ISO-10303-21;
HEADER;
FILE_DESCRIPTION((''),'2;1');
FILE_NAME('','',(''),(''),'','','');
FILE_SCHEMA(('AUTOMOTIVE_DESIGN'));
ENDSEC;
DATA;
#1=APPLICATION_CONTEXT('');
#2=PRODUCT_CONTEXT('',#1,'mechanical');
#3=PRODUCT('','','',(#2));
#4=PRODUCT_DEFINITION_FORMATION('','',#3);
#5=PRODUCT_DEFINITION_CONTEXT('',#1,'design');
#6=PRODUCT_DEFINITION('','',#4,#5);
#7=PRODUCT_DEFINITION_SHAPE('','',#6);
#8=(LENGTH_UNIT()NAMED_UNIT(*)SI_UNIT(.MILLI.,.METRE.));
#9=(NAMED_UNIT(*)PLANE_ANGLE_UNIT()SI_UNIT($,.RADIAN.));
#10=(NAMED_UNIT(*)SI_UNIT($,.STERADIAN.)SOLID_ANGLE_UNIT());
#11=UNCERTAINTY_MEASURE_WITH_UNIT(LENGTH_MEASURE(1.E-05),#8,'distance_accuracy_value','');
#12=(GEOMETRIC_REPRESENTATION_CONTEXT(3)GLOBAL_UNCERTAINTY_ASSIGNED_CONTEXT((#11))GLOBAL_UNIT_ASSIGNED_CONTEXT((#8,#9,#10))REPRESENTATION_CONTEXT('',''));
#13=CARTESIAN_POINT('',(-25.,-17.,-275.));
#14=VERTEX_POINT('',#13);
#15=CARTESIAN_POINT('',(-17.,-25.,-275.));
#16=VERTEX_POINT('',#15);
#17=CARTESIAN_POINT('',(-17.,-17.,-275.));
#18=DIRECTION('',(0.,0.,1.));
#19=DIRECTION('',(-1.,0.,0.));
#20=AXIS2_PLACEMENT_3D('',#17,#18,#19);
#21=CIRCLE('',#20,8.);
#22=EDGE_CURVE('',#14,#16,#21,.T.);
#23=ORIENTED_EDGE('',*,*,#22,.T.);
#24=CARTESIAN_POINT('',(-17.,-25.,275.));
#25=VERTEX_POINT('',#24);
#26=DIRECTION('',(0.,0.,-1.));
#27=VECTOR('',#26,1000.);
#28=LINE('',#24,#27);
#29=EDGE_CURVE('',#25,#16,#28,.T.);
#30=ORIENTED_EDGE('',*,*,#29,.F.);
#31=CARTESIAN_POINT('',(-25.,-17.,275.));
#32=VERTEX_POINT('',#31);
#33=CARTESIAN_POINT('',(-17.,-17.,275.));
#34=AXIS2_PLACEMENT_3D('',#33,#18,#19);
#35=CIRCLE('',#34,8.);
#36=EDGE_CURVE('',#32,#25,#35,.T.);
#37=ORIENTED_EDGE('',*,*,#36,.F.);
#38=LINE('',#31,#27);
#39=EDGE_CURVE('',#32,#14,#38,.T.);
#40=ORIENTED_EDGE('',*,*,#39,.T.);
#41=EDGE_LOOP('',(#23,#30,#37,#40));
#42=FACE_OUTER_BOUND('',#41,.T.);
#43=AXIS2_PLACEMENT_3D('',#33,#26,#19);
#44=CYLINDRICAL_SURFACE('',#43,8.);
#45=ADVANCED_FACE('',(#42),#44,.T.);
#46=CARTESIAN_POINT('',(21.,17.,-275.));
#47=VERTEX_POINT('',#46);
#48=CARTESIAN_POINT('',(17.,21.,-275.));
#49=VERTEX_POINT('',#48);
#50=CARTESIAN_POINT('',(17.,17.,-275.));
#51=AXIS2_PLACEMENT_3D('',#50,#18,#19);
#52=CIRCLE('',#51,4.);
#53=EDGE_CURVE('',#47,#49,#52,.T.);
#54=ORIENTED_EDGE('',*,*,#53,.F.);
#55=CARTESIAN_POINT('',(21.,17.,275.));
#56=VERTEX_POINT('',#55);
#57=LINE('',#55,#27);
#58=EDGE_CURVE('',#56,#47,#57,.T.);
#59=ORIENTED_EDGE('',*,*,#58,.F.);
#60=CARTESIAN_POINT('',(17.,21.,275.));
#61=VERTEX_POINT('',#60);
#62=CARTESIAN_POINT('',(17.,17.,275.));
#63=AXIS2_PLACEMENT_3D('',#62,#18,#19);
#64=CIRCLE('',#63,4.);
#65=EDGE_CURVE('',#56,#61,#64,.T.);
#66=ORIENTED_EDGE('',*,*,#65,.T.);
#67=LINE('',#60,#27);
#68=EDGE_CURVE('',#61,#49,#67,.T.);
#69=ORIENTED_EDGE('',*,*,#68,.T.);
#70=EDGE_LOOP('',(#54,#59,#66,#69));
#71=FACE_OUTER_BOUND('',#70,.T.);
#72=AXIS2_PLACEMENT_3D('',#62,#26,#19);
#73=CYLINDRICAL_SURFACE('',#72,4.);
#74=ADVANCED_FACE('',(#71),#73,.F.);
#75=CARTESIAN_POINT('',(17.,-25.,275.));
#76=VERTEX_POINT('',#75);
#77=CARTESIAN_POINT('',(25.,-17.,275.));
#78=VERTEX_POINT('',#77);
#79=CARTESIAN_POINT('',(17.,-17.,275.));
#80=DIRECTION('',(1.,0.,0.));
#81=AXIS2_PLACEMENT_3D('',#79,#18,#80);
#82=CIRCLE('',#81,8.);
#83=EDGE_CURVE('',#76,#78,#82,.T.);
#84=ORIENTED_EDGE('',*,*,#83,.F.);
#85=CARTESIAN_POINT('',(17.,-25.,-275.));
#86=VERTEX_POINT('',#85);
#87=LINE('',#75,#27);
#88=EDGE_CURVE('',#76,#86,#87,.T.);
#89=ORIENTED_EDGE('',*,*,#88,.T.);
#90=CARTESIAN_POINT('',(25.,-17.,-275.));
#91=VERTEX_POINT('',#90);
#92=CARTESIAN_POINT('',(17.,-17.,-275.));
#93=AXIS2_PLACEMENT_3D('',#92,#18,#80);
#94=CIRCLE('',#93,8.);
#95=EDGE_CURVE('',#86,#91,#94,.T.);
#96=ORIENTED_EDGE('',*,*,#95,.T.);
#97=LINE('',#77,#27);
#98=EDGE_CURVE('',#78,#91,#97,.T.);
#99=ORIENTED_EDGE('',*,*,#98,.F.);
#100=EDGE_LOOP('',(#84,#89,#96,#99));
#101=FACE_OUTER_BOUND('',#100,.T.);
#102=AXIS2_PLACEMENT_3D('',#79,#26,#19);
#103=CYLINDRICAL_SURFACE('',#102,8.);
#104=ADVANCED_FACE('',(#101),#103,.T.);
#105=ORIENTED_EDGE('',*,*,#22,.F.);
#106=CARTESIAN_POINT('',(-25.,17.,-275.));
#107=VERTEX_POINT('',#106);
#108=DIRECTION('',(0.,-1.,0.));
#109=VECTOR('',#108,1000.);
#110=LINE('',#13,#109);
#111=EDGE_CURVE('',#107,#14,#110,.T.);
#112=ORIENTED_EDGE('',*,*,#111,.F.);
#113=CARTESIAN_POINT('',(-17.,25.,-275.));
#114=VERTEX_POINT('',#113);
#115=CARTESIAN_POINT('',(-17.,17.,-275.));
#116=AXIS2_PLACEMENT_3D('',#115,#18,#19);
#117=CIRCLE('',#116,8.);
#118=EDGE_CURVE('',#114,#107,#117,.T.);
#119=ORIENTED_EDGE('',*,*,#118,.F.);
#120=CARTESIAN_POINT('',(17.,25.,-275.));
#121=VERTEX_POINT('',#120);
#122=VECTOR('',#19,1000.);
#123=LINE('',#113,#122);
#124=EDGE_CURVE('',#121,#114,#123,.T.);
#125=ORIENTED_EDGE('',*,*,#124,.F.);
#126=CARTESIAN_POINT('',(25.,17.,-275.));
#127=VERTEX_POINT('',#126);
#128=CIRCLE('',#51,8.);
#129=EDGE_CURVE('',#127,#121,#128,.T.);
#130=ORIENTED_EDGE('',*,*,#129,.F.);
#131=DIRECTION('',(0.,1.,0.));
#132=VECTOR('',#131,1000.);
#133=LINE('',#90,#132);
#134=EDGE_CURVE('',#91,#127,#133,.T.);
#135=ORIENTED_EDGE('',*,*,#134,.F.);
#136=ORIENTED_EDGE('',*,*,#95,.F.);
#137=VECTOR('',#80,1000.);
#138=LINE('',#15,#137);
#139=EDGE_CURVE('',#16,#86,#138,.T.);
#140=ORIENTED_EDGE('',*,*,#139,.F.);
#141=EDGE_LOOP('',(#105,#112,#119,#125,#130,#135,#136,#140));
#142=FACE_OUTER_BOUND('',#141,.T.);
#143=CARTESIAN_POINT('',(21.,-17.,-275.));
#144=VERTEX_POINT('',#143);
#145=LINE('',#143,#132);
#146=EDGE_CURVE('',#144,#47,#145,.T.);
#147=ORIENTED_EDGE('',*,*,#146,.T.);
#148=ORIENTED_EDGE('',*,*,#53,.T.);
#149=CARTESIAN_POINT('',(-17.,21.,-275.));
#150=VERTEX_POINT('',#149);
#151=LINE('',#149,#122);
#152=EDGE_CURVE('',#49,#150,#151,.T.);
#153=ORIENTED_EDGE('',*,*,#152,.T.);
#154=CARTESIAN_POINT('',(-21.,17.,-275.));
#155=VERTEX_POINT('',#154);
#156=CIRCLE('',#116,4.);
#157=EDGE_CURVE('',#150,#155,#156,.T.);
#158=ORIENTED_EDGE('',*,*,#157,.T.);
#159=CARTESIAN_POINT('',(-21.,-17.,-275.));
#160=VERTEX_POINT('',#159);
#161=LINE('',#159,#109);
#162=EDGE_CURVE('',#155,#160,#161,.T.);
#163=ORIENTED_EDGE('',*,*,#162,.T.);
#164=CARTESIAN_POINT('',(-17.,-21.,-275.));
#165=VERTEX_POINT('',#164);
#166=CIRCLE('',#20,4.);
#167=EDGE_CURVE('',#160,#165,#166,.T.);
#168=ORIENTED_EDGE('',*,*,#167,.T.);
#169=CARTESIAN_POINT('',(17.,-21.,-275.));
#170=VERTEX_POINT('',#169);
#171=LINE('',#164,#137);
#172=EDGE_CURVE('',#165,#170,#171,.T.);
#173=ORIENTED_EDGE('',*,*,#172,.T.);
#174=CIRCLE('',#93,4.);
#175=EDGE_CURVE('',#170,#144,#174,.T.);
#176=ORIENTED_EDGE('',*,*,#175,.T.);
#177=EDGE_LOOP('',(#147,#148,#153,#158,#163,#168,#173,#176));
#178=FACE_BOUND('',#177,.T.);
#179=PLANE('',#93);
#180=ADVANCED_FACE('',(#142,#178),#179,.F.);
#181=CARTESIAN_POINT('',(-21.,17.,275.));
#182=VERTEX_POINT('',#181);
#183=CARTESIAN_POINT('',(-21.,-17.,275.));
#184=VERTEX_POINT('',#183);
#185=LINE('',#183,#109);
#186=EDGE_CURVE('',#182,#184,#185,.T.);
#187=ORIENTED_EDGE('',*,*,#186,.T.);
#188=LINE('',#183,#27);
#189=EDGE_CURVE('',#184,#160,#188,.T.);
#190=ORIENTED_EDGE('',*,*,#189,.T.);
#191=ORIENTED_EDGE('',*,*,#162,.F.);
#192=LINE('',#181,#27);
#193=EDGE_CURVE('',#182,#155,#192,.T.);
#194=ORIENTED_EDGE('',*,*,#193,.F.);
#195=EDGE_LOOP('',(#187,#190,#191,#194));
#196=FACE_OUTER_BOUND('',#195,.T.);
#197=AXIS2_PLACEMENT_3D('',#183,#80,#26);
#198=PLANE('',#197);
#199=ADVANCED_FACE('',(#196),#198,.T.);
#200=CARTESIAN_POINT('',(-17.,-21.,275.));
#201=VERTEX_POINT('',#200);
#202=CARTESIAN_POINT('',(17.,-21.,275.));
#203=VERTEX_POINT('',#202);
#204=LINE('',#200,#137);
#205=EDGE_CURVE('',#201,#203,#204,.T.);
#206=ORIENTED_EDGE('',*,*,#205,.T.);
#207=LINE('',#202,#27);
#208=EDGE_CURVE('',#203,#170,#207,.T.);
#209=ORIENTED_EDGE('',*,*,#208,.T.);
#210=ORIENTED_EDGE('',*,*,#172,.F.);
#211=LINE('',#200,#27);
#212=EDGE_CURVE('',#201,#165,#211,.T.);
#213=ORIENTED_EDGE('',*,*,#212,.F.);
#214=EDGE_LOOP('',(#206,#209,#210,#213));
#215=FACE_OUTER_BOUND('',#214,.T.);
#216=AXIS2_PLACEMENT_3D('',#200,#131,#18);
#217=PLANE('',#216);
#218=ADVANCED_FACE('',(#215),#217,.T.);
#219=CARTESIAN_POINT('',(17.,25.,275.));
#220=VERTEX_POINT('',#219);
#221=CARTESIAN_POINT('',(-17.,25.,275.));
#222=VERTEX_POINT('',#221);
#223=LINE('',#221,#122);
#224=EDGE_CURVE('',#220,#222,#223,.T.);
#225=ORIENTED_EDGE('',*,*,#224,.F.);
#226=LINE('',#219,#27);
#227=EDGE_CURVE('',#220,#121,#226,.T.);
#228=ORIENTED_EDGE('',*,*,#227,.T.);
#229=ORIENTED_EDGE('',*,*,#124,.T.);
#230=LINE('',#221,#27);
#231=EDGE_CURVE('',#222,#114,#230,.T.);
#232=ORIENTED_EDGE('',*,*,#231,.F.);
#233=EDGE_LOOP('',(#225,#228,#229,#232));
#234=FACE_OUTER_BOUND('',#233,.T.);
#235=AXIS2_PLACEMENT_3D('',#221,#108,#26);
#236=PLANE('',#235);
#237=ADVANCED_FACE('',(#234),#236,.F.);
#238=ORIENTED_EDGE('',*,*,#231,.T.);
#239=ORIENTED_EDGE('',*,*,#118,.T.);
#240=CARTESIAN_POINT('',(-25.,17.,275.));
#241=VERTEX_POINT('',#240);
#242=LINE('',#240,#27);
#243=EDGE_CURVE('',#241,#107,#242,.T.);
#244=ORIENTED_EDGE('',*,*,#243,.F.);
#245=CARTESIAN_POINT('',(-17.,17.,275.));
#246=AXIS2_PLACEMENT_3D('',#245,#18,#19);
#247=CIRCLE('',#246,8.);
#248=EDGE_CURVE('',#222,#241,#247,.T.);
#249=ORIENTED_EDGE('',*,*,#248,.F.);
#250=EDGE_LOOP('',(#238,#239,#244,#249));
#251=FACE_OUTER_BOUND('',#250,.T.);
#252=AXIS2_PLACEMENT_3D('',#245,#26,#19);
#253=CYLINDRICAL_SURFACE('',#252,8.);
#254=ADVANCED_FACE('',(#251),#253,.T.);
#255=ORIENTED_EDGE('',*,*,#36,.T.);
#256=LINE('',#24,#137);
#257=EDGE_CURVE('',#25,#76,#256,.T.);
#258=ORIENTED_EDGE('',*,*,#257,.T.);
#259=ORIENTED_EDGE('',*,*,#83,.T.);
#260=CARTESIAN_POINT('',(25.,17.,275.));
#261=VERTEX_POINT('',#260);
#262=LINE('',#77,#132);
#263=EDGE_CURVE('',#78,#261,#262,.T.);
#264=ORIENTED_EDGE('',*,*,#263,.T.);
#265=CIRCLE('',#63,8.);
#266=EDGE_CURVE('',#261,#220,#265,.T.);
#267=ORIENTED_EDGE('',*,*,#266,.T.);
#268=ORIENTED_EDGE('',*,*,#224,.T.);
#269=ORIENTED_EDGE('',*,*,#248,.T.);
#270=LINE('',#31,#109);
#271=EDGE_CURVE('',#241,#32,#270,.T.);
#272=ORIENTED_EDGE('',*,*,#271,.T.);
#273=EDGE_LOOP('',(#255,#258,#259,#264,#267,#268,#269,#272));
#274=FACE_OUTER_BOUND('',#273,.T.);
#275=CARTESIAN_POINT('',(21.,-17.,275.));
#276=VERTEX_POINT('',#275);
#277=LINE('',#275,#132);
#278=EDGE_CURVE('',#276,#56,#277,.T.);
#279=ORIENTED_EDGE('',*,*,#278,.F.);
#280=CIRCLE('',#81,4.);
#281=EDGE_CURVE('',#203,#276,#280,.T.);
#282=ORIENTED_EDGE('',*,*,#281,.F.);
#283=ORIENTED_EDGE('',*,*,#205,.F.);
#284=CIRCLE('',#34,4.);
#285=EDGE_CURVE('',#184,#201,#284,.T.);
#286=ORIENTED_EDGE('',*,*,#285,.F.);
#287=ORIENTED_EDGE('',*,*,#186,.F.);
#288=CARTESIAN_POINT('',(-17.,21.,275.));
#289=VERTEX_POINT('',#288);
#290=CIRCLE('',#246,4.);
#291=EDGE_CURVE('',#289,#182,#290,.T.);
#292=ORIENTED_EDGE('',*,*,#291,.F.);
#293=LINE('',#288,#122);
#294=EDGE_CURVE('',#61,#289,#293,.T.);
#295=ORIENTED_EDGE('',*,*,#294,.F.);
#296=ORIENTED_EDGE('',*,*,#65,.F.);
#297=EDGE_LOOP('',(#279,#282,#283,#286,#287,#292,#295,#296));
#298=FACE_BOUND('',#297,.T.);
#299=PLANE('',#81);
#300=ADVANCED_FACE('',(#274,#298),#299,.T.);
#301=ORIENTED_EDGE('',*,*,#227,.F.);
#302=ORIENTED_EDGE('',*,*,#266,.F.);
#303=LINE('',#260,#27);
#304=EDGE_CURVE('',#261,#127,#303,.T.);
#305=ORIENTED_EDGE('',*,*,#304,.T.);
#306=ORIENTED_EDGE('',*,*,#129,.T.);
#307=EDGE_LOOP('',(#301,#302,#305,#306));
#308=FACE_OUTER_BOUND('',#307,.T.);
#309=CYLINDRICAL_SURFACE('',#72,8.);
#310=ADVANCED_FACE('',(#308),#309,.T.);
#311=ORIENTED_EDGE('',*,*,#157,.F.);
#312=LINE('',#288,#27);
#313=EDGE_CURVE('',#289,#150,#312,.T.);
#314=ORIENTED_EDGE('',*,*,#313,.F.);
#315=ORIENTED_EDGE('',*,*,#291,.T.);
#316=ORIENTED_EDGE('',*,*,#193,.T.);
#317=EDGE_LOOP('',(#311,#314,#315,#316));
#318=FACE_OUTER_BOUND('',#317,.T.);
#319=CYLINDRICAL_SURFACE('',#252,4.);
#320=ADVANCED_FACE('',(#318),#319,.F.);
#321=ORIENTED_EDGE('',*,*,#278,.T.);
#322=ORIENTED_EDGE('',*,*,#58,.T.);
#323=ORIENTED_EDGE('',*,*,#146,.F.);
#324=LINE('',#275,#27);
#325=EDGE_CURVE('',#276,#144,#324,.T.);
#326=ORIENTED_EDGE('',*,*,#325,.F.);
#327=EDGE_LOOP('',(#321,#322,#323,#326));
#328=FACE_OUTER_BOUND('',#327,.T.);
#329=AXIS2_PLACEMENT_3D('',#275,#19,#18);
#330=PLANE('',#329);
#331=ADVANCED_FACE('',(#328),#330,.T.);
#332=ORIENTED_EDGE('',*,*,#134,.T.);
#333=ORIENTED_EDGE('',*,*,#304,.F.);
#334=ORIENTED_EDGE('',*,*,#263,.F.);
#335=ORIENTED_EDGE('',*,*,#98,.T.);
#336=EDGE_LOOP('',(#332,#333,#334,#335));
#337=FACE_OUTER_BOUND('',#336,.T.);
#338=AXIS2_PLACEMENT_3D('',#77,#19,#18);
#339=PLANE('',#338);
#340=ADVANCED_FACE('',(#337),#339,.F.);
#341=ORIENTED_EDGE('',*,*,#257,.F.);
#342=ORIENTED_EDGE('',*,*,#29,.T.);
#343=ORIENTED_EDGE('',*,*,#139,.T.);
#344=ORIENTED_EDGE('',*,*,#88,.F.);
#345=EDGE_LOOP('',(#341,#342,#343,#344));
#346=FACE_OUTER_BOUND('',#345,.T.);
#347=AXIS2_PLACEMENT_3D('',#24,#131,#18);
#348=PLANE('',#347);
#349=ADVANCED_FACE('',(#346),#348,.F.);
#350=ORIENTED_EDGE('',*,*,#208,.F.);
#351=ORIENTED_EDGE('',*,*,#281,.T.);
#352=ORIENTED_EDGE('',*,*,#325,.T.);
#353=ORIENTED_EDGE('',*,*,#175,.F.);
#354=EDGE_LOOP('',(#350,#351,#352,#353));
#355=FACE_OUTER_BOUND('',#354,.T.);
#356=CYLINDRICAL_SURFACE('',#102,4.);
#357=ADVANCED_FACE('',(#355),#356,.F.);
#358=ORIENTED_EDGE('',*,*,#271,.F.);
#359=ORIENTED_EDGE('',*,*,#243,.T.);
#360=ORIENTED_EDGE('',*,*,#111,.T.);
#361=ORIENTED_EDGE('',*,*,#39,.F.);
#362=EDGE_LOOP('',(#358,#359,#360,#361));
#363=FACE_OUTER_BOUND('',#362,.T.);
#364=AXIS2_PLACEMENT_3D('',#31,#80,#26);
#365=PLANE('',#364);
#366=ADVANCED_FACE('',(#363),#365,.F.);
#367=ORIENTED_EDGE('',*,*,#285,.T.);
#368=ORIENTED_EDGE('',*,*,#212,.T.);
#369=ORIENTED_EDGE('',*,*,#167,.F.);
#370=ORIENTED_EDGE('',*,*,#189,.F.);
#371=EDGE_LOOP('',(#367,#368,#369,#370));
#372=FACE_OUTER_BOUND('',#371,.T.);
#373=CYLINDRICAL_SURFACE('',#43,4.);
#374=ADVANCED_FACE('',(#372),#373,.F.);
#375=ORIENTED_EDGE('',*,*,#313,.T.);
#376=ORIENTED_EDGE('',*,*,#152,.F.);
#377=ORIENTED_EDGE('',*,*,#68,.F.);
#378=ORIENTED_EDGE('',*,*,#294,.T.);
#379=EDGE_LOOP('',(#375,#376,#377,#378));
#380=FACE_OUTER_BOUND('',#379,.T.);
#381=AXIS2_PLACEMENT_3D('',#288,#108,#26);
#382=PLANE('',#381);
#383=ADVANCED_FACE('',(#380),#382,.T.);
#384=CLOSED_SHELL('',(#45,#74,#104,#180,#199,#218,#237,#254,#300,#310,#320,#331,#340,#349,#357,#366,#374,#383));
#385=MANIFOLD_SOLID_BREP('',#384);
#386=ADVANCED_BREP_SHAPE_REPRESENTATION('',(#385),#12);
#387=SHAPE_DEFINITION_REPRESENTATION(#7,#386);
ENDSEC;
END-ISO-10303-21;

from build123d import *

# Parameters (mm, degrees)
BOSS_EXTRUDE1_DEPTH = 275


with BuildPart() as part:
    # Sketch1 → Boss-Extrude1 (new, symmetric)
    with BuildSketch(Plane.XY):
        with BuildLine():
            Line((-17, -25), (17, -25))
            ThreePointArc((17, -25), (22.656854249, -22.656854249), (25, -17))
            Line((25, -17), (25, 17))
            ThreePointArc((25, 17), (22.656854249, 22.656854249), (17, 25))
            Line((17, 25), (-17, 25))
            ThreePointArc((-17, 25), (-22.656854249, 22.656854249), (-25, 17))
            Line((-25, 17), (-25, -17))
            ThreePointArc((-25, -17), (-22.656854249, -22.656854249), (-17, -25))
        make_face()
        with BuildLine():
            Line((-17, 21), (17, 21))
            ThreePointArc((17, 21), (19.828427125, 19.828427125), (21, 17))
            Line((21, 17), (21, -17))
            ThreePointArc((21, -17), (19.828427125, -19.828427125), (17, -21))
            Line((17, -21), (-17, -21))
            ThreePointArc((-17, -21), (-19.828427125, -19.828427125), (-21, -17))
            Line((-21, -17), (-21, 17))
            ThreePointArc((-21, 17), (-19.828427125, 19.828427125), (-17, 21))
        make_face(mode=Mode.SUBTRACT)
    extrude(amount=BOSS_EXTRUDE1_DEPTH, both=True)


solid = part.part
